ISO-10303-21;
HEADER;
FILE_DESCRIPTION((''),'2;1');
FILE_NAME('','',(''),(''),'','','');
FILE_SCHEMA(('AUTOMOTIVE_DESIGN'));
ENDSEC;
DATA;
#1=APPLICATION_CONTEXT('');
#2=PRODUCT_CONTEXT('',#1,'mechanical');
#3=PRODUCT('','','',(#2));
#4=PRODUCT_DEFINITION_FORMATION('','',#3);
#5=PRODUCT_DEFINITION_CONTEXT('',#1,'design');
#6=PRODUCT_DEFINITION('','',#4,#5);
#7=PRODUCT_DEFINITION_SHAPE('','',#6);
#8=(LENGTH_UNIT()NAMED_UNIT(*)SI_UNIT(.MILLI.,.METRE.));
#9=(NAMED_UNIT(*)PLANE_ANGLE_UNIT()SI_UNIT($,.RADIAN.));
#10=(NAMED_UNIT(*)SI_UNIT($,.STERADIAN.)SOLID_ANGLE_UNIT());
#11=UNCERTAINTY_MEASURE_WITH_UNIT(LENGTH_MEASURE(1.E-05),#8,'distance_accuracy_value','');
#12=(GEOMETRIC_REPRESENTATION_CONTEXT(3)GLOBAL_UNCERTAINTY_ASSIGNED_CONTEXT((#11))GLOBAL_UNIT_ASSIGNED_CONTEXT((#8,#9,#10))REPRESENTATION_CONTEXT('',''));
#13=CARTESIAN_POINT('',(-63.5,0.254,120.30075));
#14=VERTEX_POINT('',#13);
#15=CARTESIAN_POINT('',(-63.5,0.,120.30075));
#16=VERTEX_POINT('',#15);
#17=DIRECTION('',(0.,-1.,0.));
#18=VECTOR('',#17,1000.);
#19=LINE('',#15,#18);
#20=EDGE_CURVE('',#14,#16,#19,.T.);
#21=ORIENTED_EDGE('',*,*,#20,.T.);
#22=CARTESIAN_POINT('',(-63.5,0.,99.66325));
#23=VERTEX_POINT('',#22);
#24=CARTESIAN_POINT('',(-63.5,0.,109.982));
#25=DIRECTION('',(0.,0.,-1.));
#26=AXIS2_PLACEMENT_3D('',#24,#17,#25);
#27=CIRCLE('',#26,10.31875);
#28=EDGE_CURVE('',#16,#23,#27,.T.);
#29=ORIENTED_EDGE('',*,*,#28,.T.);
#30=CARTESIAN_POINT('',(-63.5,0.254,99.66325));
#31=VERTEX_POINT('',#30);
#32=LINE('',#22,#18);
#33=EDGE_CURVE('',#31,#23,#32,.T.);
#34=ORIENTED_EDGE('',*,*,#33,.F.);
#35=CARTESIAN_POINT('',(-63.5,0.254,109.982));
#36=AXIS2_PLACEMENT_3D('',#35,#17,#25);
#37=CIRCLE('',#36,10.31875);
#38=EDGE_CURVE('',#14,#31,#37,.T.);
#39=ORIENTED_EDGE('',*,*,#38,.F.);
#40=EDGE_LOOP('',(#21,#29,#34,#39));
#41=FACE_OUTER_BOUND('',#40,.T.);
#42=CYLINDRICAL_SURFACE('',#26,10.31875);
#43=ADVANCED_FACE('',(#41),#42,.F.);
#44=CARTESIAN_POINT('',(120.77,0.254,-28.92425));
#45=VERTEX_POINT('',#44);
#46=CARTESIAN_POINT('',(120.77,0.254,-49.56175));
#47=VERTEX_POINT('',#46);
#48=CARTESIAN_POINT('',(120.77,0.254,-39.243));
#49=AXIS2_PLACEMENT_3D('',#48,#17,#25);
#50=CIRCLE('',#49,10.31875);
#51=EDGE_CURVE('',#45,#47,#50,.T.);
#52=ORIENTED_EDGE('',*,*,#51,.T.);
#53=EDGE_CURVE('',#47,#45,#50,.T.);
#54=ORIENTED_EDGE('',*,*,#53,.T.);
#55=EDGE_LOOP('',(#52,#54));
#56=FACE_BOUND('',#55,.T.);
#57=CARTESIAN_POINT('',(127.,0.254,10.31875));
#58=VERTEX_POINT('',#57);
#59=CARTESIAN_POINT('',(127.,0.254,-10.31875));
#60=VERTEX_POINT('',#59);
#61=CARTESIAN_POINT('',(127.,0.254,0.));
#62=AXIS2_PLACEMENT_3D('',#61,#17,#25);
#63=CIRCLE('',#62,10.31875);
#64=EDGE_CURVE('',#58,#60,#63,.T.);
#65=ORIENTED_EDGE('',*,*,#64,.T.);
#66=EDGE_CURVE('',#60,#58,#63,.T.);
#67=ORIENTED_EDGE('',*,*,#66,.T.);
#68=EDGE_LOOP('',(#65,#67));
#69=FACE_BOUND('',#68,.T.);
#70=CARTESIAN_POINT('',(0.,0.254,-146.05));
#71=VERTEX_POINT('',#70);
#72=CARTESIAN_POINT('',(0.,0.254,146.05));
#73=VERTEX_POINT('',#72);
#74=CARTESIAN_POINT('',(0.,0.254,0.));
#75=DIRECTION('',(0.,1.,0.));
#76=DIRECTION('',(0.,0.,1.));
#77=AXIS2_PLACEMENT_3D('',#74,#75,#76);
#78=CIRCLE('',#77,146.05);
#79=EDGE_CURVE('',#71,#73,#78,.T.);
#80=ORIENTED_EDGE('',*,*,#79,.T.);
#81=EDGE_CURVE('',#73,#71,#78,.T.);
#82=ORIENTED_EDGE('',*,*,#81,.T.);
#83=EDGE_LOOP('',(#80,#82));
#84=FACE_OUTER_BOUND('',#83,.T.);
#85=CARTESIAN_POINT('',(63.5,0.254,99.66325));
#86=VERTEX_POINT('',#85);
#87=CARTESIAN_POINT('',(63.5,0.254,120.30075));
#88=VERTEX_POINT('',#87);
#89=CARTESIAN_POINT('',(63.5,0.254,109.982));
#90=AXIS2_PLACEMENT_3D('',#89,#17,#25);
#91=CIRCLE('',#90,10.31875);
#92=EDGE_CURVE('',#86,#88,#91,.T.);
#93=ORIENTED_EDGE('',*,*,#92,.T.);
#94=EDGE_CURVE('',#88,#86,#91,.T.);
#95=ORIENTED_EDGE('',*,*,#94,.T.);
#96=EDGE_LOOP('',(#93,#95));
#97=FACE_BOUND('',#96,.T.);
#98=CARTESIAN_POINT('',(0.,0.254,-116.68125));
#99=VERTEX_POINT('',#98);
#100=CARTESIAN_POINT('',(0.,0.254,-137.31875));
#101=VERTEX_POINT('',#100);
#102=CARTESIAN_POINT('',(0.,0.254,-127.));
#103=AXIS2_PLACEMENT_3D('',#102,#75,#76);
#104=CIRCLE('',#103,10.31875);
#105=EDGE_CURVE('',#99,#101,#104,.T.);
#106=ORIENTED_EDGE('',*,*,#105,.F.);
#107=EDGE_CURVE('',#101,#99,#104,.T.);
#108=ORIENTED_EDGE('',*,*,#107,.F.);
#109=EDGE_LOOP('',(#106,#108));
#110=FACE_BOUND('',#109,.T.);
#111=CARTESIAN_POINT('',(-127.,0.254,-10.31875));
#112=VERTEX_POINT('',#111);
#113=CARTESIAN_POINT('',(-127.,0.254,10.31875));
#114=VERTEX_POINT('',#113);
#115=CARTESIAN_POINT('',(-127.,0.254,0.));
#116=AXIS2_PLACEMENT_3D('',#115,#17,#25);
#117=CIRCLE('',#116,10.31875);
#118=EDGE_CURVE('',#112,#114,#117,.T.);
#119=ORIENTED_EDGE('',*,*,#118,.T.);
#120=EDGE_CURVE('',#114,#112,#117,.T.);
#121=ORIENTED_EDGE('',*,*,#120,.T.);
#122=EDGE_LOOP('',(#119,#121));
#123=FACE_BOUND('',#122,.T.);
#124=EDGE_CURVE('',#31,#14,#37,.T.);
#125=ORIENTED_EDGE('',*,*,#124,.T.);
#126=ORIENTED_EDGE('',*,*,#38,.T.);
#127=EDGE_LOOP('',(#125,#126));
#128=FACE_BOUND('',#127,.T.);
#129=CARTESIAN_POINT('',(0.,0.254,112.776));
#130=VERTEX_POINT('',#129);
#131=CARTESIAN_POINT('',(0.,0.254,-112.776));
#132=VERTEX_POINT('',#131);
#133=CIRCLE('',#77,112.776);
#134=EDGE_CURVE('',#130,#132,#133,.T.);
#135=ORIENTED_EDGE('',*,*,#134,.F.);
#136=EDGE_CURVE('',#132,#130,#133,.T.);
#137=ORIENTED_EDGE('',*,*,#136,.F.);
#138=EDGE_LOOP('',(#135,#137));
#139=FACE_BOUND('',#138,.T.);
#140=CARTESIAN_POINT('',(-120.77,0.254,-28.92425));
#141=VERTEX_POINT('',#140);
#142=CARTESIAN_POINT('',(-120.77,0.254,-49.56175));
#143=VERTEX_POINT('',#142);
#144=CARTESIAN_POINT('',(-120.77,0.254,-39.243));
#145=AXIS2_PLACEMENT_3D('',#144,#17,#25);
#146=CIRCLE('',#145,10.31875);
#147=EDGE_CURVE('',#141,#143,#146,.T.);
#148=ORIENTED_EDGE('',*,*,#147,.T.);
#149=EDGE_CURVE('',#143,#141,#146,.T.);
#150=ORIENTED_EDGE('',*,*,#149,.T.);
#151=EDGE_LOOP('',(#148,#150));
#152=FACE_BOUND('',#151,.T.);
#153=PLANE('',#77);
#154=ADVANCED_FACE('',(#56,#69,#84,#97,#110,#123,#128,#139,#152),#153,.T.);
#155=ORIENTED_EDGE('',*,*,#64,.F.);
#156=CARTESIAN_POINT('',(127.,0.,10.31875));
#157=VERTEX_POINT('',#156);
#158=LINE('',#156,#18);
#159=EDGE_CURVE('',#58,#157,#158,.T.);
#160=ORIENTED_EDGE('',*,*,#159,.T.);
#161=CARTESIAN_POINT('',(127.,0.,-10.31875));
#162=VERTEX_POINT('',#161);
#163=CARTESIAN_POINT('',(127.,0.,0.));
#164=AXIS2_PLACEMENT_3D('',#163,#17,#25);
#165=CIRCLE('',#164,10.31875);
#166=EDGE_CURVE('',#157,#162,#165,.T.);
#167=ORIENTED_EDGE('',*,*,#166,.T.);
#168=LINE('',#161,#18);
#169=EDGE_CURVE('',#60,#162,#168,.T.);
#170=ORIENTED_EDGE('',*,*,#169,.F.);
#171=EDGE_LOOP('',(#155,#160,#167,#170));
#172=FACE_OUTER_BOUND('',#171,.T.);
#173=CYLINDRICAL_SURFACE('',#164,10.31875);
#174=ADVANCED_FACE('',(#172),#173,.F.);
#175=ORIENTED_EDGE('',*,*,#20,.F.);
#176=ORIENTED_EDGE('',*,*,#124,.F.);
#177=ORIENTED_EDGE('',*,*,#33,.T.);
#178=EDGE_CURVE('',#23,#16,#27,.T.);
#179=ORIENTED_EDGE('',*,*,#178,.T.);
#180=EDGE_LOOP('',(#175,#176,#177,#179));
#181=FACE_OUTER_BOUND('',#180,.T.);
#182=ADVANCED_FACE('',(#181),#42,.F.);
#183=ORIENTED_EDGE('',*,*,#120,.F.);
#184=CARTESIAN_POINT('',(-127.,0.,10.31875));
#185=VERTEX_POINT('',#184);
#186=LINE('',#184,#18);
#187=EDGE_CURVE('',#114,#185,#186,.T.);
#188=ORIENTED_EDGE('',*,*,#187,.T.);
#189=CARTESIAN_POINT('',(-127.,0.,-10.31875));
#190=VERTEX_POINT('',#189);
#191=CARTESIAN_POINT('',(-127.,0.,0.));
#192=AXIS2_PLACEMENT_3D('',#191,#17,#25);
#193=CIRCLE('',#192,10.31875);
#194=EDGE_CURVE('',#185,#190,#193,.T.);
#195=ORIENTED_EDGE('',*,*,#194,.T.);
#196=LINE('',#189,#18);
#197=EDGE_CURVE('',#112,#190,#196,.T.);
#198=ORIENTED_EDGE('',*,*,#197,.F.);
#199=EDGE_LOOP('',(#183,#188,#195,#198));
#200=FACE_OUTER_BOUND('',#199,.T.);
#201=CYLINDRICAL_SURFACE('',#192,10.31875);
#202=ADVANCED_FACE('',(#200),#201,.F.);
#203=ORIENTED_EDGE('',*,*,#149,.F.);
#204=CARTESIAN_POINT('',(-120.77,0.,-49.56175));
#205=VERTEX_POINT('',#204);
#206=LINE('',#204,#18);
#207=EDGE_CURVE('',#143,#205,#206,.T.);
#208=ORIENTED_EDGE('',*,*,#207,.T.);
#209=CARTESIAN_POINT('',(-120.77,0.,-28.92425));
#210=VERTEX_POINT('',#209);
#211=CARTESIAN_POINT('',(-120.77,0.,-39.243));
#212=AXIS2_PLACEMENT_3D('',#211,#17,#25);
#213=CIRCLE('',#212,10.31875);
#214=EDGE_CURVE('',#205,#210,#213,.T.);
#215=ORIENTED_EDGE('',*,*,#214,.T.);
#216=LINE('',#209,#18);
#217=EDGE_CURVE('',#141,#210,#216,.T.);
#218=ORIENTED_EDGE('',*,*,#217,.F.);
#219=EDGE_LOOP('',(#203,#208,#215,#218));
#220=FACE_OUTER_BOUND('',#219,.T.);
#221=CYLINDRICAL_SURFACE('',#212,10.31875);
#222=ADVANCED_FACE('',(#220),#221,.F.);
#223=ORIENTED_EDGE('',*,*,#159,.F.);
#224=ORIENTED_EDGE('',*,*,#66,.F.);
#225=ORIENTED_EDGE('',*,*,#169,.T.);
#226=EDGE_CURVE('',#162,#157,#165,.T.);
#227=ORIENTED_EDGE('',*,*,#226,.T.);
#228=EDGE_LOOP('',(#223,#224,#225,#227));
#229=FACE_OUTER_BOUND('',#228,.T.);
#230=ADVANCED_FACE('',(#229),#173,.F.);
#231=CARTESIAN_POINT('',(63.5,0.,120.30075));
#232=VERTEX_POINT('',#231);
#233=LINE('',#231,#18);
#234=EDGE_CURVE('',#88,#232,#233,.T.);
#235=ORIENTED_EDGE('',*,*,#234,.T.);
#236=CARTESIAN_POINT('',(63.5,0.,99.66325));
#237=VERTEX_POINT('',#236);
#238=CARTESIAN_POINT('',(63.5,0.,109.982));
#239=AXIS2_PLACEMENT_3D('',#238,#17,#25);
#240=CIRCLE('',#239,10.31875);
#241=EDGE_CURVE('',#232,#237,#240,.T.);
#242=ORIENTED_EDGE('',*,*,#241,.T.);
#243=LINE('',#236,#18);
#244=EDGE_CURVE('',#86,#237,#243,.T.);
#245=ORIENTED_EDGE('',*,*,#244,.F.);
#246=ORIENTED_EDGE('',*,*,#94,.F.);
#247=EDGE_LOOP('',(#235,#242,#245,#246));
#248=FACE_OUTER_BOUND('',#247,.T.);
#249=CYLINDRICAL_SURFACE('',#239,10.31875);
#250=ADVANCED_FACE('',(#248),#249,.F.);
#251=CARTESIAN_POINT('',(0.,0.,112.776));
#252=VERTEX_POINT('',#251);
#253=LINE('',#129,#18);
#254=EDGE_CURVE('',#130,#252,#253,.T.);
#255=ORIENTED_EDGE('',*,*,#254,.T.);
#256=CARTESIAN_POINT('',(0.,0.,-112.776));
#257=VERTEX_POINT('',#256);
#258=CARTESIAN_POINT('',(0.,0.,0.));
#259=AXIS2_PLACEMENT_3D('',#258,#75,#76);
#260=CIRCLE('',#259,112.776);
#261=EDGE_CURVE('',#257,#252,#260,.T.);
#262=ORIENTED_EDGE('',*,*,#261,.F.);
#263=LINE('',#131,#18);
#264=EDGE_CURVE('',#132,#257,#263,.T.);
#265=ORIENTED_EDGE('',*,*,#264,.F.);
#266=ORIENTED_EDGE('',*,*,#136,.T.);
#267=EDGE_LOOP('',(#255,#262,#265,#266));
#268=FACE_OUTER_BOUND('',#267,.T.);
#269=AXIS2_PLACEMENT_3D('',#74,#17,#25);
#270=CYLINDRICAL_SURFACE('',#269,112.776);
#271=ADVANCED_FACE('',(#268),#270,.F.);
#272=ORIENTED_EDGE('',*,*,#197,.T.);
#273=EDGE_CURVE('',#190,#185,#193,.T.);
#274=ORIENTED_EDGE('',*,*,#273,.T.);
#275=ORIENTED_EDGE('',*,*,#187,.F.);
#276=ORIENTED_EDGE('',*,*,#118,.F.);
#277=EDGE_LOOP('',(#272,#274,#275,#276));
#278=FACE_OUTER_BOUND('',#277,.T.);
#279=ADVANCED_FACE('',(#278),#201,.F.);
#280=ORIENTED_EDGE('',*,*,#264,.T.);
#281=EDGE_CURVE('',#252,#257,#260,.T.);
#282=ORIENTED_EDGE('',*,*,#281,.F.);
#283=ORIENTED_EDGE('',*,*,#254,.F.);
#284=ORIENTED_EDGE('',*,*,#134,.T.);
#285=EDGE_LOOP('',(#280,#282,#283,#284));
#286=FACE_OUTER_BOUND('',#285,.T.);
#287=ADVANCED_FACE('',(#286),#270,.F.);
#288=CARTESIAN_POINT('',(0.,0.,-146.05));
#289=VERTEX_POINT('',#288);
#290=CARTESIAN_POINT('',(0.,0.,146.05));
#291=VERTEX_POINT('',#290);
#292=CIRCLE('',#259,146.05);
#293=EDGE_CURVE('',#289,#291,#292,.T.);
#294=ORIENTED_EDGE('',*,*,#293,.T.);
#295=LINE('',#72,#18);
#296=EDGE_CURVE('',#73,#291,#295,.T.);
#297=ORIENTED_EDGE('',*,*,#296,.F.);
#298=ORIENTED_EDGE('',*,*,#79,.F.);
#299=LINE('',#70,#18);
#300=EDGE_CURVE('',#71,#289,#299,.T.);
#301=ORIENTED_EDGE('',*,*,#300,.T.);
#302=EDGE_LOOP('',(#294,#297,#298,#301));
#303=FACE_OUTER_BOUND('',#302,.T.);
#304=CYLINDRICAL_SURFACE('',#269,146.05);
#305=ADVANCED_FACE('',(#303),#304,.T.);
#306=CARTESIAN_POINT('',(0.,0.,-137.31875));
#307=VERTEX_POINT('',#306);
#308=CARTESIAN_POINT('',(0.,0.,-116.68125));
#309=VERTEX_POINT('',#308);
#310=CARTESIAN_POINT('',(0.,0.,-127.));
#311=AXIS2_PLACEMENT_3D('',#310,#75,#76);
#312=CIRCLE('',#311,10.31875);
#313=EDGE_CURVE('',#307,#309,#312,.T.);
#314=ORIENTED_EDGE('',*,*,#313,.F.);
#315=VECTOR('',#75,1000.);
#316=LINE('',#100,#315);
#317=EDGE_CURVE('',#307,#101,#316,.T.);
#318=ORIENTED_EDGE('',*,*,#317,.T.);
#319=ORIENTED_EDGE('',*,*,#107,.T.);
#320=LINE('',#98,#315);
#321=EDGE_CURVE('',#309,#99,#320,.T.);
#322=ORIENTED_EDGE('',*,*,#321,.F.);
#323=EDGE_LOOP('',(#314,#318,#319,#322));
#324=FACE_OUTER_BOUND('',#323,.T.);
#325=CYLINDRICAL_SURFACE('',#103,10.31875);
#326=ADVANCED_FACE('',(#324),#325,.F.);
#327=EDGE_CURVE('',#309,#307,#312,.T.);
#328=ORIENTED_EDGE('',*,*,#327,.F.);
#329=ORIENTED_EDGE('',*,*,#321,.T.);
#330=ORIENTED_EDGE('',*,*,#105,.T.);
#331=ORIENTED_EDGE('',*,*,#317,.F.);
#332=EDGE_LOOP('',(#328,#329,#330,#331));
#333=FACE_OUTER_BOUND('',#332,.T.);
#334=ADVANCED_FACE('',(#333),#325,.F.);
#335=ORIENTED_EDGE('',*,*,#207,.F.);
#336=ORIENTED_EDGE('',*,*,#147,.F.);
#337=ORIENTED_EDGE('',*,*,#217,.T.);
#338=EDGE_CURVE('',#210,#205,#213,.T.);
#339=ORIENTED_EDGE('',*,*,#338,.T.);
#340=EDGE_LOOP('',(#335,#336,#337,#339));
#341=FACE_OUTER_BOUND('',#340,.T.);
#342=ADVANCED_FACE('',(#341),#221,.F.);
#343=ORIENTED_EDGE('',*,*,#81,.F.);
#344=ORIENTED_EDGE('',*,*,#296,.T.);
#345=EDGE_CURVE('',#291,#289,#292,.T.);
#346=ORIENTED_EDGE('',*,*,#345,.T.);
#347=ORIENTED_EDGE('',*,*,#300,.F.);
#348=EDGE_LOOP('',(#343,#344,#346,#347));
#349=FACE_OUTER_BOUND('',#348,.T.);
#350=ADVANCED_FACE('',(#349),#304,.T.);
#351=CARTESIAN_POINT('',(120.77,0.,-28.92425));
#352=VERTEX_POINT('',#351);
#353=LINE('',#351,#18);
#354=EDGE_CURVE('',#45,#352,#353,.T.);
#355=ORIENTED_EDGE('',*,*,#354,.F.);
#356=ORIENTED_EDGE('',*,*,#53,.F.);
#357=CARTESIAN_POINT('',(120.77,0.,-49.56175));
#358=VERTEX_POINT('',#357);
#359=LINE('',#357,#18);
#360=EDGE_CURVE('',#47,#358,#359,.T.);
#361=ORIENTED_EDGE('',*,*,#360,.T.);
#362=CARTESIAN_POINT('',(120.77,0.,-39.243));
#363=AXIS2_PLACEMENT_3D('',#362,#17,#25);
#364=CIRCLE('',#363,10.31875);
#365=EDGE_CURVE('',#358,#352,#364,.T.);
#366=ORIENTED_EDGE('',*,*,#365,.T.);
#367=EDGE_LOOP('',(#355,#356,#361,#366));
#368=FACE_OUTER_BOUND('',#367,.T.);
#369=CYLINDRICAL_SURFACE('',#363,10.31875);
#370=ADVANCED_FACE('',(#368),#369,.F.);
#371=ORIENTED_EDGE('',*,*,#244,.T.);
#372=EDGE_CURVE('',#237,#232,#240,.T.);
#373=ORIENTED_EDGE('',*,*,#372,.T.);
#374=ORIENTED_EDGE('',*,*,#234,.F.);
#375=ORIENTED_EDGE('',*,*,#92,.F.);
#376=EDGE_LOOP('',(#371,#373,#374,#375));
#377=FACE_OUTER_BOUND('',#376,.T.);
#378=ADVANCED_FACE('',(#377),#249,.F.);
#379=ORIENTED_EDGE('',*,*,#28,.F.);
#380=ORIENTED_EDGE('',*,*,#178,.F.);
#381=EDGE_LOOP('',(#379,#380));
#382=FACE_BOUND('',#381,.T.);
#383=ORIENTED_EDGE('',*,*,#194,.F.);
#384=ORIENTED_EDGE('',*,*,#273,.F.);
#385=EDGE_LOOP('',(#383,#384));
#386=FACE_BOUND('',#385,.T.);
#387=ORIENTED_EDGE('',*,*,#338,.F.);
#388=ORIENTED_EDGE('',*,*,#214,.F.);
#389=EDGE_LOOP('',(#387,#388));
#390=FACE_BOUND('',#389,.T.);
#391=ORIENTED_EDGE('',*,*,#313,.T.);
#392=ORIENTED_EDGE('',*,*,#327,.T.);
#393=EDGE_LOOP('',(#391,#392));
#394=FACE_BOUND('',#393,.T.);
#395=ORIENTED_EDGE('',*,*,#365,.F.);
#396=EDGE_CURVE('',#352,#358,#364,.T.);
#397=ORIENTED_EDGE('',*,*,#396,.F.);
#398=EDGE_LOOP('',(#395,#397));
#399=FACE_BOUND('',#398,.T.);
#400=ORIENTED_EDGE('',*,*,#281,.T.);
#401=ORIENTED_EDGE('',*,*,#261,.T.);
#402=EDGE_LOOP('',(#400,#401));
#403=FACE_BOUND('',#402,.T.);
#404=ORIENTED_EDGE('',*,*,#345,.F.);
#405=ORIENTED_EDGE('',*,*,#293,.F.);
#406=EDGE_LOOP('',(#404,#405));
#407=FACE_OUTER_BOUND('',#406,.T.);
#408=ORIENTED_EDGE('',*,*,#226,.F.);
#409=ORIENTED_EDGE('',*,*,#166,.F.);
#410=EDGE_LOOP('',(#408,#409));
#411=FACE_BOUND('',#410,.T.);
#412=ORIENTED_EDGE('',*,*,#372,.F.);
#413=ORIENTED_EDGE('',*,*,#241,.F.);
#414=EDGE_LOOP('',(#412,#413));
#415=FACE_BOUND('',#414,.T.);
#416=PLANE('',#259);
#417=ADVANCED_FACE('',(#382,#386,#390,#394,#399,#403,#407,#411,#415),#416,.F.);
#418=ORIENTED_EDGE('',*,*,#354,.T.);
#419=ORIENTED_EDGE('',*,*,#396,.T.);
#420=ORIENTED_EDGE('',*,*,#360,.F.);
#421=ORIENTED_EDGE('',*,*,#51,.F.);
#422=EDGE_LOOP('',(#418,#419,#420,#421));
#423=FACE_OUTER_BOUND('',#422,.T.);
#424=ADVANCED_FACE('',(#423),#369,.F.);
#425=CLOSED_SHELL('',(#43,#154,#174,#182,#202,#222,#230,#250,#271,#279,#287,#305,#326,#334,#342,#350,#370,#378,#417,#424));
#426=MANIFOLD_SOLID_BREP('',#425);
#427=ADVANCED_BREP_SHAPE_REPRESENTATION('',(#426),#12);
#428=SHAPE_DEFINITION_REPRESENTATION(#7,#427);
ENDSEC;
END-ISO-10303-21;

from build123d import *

# Parameters (mm, degrees)
SKETCH1_R                       = 146.05
SKETCH1_R_2                     = 112.776
BOSS_EXTRUDE1_DEPTH             = 0.254
F_13_16_0_8125_DIAMETER_HOLE1_D = 20.6375
F_13_16_0_8125_DIAMETER_HOLE2_D = 20.6375


with BuildPart() as part:
    # Sketch1 → Boss-Extrude1 (new body)
    with BuildSketch(Plane(origin=(0, 0, 0), x_dir=(1, 0, 0), z_dir=(0, 1, 0))):
        with Locations(Location((0, 0, 0), (0, 0, 270))):
            Circle(SKETCH1_R)
        with Locations(Location((0, 0, 0), (0, 0, 270))):
            Circle(SKETCH1_R_2, mode=Mode.SUBTRACT)
    extrude(amount=BOSS_EXTRUDE1_DEPTH)

    # 13/16 (0.8125) Diameter Hole1 (through all)
    with Locations(Plane(origin=(0, 0.254, 0), x_dir=(1, 0, 0), z_dir=(0, 1, 0))):
        with Locations((0, 127)):
            Hole(F_13_16_0_8125_DIAMETER_HOLE1_D / 2)

    # 13/16 (0.8125) Diameter Hole2 (through all)
    with Locations(Plane(origin=(0, 0, 0), x_dir=(-1, 0, 0), z_dir=(0, -1, 0))):
        with Locations((-63.5, -109.982), (-120.77, 39.243), (-127, 0)):
            f_13_16_0_8125_diameter_hole2 = Hole(F_13_16_0_8125_DIAMETER_HOLE2_D / 2)

    # Mirror1: 13/16 (0.8125) Diameter Hole2 across plane
    add(f_13_16_0_8125_diameter_hole2.mirror(Plane(origin=(0, 0, 0), x_dir=(0, 0, 1), z_dir=(1, 0, 0))), mode=Mode.SUBTRACT)


solid = part.part
